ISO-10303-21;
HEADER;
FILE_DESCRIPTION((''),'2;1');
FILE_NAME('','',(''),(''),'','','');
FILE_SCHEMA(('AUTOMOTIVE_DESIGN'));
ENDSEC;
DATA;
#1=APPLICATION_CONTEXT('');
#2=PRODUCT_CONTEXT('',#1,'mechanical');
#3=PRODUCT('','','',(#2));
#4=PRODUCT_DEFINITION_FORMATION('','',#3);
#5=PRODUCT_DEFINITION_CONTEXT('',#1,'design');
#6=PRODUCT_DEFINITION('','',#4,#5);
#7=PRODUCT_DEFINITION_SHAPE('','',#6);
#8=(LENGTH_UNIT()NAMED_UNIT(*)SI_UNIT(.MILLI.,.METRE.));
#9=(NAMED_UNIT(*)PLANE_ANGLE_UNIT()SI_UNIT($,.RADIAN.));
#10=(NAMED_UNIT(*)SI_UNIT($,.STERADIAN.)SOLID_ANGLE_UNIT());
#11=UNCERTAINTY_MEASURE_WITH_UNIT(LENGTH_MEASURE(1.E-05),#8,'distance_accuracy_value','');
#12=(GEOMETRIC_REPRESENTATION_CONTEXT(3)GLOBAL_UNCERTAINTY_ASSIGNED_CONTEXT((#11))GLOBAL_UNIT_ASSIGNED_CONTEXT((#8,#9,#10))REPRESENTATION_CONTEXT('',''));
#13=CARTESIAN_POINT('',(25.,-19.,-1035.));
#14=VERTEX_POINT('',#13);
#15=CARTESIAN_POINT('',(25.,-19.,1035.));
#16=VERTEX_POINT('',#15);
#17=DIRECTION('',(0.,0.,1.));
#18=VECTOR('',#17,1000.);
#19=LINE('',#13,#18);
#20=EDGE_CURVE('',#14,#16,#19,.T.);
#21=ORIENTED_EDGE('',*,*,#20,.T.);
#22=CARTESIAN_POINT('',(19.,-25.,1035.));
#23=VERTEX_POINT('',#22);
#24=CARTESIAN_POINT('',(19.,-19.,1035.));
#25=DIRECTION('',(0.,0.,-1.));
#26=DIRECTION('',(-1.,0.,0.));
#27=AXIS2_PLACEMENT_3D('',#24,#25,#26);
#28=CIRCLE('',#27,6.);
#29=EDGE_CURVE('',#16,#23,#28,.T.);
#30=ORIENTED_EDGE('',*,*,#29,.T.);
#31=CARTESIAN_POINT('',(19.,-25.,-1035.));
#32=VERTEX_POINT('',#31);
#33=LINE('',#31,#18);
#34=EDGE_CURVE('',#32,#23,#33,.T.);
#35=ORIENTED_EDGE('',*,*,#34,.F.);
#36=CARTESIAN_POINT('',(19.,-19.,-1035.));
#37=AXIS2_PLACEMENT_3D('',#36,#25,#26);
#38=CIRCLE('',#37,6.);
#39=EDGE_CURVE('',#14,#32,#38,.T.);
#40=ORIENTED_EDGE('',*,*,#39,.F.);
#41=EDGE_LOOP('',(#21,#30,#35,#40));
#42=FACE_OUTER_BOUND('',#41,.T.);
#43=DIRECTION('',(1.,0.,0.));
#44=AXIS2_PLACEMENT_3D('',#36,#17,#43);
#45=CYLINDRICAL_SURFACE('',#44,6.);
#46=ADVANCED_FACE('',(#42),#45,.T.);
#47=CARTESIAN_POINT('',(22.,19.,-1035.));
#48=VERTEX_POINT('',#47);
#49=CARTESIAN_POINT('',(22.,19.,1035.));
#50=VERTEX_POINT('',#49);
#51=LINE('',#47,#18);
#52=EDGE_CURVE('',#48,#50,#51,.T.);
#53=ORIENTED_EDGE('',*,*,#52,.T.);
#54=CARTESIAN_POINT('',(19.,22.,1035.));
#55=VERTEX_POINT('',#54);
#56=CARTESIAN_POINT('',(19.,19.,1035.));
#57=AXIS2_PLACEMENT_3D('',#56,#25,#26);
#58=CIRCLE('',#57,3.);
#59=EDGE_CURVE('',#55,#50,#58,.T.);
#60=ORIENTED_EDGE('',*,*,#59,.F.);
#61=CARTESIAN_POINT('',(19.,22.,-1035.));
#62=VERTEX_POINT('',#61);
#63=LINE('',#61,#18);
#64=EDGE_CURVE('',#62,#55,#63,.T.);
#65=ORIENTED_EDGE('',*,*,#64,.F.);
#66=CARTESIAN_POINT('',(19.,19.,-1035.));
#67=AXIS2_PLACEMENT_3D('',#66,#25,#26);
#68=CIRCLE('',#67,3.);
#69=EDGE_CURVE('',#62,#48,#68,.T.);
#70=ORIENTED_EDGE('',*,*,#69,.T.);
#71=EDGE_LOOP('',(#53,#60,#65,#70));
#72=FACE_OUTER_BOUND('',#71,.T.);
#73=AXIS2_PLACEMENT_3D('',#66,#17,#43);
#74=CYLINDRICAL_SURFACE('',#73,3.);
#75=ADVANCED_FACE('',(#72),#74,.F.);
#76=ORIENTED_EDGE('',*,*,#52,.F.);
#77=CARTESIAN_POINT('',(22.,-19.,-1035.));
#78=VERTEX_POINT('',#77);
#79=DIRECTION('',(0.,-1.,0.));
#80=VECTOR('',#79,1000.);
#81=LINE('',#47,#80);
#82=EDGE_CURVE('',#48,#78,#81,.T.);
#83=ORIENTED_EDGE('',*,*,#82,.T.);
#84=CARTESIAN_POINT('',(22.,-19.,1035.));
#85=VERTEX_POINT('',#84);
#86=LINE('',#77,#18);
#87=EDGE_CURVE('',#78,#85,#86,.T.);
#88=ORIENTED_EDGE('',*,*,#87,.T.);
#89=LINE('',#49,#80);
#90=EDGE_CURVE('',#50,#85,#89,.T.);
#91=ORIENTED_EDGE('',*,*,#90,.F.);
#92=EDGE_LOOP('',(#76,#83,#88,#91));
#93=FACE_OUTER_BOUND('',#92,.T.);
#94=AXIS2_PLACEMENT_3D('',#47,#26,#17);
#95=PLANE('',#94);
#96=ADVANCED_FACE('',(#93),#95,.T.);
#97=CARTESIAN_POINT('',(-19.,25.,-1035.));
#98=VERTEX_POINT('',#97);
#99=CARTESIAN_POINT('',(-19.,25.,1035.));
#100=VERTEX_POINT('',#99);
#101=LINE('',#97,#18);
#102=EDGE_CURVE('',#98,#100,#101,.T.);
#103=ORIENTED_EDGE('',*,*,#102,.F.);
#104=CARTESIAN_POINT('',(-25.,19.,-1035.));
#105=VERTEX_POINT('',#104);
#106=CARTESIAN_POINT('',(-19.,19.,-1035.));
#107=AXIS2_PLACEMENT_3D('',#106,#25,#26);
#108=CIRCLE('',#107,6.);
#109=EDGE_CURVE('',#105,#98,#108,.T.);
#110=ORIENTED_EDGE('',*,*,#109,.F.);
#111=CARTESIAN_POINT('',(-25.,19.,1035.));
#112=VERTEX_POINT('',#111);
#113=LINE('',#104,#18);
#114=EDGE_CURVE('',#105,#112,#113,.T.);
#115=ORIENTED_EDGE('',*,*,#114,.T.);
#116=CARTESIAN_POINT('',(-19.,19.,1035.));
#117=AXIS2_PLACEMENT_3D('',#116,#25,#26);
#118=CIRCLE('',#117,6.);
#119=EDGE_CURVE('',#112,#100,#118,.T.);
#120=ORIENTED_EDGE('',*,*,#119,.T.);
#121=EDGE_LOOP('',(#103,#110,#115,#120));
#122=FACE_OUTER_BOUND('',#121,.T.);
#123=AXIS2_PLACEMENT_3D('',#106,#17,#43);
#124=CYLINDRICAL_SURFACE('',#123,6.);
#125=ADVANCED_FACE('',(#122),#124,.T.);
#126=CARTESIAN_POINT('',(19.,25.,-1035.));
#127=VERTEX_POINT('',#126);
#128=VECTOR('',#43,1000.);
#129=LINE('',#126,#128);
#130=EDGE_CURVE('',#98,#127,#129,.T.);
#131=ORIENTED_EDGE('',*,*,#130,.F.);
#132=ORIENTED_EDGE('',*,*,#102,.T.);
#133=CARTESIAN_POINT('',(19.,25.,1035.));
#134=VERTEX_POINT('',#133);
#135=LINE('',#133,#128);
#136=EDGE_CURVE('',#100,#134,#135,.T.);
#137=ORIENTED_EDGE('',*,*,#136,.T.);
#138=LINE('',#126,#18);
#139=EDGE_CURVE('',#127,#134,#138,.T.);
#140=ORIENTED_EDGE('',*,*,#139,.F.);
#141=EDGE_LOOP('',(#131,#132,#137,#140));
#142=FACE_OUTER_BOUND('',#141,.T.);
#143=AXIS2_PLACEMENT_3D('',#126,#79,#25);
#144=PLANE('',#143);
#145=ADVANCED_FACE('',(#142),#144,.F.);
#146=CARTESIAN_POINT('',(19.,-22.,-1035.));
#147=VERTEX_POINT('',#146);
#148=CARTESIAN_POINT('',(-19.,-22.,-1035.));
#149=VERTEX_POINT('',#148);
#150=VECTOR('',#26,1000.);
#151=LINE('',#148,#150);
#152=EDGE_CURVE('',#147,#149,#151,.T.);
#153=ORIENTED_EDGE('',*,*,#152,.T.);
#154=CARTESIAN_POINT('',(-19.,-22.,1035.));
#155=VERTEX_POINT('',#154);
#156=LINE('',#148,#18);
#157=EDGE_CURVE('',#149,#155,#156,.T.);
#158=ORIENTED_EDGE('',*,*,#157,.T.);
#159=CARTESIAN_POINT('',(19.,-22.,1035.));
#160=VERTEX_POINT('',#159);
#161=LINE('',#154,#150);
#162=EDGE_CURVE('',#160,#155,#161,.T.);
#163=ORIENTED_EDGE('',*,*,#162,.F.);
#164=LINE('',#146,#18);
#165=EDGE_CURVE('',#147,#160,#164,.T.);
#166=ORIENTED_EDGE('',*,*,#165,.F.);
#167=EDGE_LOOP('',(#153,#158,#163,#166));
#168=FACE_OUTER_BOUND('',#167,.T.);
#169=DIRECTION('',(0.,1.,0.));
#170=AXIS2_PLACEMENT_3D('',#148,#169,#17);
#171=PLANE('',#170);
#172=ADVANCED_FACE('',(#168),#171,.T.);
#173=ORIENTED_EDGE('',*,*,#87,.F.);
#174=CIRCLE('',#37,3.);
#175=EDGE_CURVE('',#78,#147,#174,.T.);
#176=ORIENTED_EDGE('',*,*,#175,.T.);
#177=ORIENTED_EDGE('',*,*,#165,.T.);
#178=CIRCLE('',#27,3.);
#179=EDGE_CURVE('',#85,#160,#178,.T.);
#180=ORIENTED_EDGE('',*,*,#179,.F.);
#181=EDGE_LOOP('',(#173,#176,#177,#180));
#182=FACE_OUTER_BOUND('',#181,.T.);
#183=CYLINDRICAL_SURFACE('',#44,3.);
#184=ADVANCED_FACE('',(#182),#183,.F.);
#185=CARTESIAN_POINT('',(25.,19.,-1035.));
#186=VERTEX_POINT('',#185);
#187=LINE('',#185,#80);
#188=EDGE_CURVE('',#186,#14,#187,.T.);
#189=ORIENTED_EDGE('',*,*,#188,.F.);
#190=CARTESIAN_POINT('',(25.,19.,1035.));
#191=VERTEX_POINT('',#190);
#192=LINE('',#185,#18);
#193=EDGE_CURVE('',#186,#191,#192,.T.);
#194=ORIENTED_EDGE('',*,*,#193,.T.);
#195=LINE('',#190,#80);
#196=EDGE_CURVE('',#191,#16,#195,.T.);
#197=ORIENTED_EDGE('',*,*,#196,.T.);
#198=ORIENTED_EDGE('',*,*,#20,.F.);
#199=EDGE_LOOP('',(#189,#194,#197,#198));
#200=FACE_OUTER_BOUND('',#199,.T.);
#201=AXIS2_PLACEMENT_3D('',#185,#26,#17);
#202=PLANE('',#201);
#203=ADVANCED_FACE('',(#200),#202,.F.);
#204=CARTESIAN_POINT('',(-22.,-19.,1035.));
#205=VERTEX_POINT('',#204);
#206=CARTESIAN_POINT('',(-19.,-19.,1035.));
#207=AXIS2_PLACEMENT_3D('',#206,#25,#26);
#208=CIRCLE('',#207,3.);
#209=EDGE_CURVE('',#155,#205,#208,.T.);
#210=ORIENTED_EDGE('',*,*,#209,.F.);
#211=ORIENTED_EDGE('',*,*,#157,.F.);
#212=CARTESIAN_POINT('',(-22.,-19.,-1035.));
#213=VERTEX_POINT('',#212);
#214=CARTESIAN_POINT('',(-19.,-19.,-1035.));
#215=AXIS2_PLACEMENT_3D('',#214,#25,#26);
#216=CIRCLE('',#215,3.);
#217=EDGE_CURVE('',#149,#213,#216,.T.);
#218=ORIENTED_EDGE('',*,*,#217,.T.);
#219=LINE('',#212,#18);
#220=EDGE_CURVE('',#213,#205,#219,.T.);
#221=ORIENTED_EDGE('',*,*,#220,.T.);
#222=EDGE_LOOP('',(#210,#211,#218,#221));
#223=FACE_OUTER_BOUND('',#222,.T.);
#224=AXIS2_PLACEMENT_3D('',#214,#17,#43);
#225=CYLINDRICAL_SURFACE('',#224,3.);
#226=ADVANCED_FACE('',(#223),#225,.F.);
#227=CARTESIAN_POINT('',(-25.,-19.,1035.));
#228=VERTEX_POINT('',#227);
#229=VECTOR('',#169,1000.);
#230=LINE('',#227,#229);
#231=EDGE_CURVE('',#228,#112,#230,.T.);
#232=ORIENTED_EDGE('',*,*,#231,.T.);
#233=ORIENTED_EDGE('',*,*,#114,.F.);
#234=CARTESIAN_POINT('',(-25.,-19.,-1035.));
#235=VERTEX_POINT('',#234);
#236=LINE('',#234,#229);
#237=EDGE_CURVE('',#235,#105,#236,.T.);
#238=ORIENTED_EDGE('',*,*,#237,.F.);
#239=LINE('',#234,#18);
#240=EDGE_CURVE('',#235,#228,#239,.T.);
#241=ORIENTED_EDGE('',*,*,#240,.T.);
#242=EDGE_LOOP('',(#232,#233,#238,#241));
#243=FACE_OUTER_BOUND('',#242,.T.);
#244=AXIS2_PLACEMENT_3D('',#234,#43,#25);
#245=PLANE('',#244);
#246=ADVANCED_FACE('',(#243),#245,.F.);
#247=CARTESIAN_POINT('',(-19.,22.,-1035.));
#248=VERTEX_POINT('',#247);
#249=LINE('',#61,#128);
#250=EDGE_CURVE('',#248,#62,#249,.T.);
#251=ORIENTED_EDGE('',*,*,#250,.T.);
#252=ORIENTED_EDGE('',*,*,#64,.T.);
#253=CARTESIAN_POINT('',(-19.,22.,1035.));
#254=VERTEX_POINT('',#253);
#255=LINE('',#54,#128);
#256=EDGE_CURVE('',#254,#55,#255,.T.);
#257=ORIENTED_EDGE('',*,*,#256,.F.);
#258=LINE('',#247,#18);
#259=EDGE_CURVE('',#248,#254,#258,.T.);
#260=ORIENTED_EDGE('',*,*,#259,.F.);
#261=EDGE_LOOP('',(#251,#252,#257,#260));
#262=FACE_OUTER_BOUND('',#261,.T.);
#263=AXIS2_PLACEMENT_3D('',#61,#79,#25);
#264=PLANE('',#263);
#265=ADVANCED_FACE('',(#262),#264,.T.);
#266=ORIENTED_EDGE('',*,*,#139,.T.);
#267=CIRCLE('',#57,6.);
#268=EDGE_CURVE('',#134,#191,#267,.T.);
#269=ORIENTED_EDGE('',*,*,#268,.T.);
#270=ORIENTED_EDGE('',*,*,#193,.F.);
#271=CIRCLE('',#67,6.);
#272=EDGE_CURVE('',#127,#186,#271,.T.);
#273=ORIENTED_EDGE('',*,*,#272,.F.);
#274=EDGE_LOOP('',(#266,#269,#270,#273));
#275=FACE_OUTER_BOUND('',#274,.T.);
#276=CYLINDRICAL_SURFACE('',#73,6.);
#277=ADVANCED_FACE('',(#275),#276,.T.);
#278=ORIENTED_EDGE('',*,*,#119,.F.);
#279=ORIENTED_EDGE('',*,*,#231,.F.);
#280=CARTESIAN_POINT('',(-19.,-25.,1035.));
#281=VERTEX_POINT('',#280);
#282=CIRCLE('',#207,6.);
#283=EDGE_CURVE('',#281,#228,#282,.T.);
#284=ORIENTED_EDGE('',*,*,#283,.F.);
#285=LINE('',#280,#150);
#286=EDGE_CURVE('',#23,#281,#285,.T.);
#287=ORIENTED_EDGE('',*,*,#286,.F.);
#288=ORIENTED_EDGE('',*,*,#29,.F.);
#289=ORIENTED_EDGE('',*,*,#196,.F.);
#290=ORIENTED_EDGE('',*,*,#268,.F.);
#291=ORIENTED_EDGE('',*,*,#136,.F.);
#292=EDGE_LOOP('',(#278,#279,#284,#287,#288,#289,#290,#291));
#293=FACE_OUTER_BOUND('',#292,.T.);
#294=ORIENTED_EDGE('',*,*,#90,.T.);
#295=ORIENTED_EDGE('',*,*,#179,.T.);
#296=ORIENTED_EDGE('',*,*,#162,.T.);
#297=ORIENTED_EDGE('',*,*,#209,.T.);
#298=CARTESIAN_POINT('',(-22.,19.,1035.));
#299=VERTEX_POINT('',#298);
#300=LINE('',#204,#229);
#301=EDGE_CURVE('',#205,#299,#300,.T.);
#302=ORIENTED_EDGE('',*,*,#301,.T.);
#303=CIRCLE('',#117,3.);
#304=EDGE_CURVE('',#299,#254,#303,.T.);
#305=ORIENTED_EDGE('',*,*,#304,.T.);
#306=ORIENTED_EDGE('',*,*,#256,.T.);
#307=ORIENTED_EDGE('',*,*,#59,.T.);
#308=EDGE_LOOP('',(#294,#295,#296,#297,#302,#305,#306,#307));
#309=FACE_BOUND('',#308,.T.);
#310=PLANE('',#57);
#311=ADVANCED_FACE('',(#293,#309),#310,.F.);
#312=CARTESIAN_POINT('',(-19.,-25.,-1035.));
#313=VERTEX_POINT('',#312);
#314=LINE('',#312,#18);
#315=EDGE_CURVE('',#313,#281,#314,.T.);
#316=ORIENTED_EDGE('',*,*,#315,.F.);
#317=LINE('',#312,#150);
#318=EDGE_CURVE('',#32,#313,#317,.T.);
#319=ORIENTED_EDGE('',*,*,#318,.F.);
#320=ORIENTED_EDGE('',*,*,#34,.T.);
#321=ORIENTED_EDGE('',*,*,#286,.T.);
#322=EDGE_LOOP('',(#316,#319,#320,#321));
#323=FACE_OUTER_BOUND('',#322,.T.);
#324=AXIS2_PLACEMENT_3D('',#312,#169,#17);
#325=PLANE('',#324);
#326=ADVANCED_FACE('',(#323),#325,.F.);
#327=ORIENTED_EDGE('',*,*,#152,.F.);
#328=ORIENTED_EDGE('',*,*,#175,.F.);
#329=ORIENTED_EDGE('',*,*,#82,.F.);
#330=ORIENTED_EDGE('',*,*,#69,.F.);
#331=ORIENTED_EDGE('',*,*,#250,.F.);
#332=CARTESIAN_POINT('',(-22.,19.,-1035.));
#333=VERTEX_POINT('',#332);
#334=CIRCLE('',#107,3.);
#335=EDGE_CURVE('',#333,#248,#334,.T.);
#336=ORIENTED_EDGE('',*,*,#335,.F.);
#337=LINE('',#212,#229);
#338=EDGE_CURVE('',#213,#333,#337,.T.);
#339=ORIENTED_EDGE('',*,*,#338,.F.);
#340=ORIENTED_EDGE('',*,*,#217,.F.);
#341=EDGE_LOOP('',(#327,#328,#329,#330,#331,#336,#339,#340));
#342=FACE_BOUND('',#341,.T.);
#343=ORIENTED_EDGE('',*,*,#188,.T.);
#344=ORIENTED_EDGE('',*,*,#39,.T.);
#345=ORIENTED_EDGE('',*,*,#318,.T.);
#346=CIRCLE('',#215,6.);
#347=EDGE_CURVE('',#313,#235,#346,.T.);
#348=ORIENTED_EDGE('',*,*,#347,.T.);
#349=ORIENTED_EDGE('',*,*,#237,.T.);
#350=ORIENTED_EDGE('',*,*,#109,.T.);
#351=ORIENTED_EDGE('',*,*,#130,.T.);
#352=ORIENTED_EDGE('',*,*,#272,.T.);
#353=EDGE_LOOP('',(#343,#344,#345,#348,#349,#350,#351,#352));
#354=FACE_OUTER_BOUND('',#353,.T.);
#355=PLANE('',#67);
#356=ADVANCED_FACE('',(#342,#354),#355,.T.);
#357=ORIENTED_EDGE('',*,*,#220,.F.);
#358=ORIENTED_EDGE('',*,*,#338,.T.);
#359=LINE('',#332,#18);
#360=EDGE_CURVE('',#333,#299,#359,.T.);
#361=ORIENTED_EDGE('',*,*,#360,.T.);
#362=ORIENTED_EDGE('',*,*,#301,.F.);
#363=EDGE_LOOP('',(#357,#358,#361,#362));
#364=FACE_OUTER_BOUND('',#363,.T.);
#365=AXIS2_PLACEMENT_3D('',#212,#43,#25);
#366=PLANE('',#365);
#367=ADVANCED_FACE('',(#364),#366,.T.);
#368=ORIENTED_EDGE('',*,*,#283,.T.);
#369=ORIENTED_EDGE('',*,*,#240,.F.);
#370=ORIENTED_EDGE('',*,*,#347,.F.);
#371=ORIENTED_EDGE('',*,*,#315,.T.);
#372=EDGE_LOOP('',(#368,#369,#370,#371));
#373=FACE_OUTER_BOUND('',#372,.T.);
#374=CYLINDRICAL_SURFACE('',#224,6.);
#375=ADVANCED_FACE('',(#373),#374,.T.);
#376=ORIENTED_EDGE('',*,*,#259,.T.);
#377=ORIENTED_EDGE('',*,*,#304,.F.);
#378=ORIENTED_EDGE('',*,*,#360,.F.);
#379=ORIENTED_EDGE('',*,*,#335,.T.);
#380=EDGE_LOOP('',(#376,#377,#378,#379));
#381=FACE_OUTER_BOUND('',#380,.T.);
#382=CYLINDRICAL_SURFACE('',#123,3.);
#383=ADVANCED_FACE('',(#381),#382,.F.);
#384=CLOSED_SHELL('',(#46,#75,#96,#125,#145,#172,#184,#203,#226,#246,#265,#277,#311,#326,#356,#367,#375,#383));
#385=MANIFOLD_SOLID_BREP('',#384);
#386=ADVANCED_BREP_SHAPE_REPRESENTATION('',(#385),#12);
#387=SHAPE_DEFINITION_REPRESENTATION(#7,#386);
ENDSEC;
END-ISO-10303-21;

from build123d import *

# Parameters (mm, degrees)
GB_6728_1986_050_X_50_X_3_1_DEPTH = 2070


with BuildPart() as part:
    # Sketch1 → Gb／6728-1986方形空心型钢 050 X 50 X 3(1) (new body)
    with BuildSketch(Plane.YX.offset(-1035)):
        with BuildLine():
            Line((-19, -25), (19, -25))
            ThreePointArc((19, -25), (23.242640687, -23.242640687), (25, -19))
            Line((25, -19), (25, 19))
            ThreePointArc((25, 19), (23.242640687, 23.242640687), (19, 25))
            Line((19, 25), (-19, 25))
            ThreePointArc((-19, 25), (-23.242640687, 23.242640687), (-25, 19))
            Line((-25, 19), (-25, -19))
            ThreePointArc((-25, -19), (-23.242640687, -23.242640687), (-19, -25))
        make_face()
        with BuildLine():
            Line((-19, -22), (19, -22))
            ThreePointArc((19, -22), (21.121320344, -21.121320344), (22, -19))
            Line((22, -19), (22, 19))
            ThreePointArc((22, 19), (21.121320344, 21.121320344), (19, 22))
            Line((19, 22), (-19, 22))
            ThreePointArc((-19, 22), (-21.121320344, 21.121320344), (-22, 19))
            Line((-22, 19), (-22, -19))
            ThreePointArc((-22, -19), (-21.121320344, -21.121320344), (-19, -22))
        make_face(mode=Mode.SUBTRACT)
    extrude(amount=GB_6728_1986_050_X_50_X_3_1_DEPTH)


solid = part.part
